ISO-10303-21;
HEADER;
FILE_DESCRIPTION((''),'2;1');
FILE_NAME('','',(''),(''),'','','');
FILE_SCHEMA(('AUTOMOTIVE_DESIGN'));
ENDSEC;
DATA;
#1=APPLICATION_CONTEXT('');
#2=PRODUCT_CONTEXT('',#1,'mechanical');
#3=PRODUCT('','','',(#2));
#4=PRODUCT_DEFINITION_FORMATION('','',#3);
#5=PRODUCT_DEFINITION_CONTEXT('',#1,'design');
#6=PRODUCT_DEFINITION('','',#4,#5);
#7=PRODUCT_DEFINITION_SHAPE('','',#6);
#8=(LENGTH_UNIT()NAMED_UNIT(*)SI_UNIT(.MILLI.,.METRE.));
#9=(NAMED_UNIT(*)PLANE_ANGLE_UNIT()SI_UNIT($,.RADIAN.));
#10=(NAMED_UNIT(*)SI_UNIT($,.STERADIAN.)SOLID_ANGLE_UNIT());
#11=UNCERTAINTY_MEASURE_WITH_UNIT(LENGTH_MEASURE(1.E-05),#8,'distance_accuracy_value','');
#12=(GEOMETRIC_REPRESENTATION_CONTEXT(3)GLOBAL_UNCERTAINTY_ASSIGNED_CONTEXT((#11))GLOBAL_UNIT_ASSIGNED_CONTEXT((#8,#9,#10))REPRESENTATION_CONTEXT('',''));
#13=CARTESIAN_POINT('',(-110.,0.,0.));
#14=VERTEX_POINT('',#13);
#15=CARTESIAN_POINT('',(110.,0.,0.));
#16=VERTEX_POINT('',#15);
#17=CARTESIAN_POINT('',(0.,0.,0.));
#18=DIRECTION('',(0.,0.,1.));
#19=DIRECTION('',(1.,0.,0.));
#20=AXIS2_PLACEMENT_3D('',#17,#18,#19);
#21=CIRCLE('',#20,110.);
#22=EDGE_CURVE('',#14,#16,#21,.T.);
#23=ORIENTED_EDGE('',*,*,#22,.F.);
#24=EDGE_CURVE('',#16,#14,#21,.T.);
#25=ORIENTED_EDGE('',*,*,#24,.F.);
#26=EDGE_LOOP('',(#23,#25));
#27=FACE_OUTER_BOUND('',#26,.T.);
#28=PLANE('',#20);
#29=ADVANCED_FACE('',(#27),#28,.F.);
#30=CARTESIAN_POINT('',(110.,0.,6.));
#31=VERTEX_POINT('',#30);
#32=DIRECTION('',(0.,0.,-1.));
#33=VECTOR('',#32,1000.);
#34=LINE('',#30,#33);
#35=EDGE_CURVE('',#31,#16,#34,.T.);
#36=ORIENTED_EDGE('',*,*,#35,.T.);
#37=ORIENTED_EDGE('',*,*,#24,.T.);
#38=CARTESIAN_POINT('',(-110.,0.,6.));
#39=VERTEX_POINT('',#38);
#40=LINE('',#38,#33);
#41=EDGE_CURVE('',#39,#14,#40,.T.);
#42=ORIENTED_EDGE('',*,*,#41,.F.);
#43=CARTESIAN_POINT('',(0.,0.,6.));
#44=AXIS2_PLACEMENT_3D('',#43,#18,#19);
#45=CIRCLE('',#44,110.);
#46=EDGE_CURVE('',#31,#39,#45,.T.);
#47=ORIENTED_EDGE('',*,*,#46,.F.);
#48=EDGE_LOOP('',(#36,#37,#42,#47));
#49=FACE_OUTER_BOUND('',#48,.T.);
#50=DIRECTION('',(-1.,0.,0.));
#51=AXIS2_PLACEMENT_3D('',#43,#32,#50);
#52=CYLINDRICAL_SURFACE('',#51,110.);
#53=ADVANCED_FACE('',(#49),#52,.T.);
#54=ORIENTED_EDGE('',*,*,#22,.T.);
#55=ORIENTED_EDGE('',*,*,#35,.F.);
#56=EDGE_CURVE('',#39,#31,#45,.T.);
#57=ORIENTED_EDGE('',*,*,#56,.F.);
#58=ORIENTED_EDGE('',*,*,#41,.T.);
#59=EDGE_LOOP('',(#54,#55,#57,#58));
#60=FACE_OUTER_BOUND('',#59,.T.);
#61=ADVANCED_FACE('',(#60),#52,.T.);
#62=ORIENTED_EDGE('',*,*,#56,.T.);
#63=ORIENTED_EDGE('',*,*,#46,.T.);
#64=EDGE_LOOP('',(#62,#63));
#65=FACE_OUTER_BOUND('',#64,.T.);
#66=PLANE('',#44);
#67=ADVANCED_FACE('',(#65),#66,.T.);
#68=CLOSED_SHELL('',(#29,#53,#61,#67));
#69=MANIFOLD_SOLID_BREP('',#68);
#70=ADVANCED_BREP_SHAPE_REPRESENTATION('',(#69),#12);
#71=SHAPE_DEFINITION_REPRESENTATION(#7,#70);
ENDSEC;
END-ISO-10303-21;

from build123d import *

# Parameters (mm, degrees)
SKETCH1_R           = 110
BOSS_EXTRUDE1_DEPTH = 6


with BuildPart() as part:
    # Sketch1 → Boss-Extrude1 (new body)
    with BuildSketch(Plane.XY):
        Circle(SKETCH1_R)
    extrude(amount=BOSS_EXTRUDE1_DEPTH)


solid = part.part
